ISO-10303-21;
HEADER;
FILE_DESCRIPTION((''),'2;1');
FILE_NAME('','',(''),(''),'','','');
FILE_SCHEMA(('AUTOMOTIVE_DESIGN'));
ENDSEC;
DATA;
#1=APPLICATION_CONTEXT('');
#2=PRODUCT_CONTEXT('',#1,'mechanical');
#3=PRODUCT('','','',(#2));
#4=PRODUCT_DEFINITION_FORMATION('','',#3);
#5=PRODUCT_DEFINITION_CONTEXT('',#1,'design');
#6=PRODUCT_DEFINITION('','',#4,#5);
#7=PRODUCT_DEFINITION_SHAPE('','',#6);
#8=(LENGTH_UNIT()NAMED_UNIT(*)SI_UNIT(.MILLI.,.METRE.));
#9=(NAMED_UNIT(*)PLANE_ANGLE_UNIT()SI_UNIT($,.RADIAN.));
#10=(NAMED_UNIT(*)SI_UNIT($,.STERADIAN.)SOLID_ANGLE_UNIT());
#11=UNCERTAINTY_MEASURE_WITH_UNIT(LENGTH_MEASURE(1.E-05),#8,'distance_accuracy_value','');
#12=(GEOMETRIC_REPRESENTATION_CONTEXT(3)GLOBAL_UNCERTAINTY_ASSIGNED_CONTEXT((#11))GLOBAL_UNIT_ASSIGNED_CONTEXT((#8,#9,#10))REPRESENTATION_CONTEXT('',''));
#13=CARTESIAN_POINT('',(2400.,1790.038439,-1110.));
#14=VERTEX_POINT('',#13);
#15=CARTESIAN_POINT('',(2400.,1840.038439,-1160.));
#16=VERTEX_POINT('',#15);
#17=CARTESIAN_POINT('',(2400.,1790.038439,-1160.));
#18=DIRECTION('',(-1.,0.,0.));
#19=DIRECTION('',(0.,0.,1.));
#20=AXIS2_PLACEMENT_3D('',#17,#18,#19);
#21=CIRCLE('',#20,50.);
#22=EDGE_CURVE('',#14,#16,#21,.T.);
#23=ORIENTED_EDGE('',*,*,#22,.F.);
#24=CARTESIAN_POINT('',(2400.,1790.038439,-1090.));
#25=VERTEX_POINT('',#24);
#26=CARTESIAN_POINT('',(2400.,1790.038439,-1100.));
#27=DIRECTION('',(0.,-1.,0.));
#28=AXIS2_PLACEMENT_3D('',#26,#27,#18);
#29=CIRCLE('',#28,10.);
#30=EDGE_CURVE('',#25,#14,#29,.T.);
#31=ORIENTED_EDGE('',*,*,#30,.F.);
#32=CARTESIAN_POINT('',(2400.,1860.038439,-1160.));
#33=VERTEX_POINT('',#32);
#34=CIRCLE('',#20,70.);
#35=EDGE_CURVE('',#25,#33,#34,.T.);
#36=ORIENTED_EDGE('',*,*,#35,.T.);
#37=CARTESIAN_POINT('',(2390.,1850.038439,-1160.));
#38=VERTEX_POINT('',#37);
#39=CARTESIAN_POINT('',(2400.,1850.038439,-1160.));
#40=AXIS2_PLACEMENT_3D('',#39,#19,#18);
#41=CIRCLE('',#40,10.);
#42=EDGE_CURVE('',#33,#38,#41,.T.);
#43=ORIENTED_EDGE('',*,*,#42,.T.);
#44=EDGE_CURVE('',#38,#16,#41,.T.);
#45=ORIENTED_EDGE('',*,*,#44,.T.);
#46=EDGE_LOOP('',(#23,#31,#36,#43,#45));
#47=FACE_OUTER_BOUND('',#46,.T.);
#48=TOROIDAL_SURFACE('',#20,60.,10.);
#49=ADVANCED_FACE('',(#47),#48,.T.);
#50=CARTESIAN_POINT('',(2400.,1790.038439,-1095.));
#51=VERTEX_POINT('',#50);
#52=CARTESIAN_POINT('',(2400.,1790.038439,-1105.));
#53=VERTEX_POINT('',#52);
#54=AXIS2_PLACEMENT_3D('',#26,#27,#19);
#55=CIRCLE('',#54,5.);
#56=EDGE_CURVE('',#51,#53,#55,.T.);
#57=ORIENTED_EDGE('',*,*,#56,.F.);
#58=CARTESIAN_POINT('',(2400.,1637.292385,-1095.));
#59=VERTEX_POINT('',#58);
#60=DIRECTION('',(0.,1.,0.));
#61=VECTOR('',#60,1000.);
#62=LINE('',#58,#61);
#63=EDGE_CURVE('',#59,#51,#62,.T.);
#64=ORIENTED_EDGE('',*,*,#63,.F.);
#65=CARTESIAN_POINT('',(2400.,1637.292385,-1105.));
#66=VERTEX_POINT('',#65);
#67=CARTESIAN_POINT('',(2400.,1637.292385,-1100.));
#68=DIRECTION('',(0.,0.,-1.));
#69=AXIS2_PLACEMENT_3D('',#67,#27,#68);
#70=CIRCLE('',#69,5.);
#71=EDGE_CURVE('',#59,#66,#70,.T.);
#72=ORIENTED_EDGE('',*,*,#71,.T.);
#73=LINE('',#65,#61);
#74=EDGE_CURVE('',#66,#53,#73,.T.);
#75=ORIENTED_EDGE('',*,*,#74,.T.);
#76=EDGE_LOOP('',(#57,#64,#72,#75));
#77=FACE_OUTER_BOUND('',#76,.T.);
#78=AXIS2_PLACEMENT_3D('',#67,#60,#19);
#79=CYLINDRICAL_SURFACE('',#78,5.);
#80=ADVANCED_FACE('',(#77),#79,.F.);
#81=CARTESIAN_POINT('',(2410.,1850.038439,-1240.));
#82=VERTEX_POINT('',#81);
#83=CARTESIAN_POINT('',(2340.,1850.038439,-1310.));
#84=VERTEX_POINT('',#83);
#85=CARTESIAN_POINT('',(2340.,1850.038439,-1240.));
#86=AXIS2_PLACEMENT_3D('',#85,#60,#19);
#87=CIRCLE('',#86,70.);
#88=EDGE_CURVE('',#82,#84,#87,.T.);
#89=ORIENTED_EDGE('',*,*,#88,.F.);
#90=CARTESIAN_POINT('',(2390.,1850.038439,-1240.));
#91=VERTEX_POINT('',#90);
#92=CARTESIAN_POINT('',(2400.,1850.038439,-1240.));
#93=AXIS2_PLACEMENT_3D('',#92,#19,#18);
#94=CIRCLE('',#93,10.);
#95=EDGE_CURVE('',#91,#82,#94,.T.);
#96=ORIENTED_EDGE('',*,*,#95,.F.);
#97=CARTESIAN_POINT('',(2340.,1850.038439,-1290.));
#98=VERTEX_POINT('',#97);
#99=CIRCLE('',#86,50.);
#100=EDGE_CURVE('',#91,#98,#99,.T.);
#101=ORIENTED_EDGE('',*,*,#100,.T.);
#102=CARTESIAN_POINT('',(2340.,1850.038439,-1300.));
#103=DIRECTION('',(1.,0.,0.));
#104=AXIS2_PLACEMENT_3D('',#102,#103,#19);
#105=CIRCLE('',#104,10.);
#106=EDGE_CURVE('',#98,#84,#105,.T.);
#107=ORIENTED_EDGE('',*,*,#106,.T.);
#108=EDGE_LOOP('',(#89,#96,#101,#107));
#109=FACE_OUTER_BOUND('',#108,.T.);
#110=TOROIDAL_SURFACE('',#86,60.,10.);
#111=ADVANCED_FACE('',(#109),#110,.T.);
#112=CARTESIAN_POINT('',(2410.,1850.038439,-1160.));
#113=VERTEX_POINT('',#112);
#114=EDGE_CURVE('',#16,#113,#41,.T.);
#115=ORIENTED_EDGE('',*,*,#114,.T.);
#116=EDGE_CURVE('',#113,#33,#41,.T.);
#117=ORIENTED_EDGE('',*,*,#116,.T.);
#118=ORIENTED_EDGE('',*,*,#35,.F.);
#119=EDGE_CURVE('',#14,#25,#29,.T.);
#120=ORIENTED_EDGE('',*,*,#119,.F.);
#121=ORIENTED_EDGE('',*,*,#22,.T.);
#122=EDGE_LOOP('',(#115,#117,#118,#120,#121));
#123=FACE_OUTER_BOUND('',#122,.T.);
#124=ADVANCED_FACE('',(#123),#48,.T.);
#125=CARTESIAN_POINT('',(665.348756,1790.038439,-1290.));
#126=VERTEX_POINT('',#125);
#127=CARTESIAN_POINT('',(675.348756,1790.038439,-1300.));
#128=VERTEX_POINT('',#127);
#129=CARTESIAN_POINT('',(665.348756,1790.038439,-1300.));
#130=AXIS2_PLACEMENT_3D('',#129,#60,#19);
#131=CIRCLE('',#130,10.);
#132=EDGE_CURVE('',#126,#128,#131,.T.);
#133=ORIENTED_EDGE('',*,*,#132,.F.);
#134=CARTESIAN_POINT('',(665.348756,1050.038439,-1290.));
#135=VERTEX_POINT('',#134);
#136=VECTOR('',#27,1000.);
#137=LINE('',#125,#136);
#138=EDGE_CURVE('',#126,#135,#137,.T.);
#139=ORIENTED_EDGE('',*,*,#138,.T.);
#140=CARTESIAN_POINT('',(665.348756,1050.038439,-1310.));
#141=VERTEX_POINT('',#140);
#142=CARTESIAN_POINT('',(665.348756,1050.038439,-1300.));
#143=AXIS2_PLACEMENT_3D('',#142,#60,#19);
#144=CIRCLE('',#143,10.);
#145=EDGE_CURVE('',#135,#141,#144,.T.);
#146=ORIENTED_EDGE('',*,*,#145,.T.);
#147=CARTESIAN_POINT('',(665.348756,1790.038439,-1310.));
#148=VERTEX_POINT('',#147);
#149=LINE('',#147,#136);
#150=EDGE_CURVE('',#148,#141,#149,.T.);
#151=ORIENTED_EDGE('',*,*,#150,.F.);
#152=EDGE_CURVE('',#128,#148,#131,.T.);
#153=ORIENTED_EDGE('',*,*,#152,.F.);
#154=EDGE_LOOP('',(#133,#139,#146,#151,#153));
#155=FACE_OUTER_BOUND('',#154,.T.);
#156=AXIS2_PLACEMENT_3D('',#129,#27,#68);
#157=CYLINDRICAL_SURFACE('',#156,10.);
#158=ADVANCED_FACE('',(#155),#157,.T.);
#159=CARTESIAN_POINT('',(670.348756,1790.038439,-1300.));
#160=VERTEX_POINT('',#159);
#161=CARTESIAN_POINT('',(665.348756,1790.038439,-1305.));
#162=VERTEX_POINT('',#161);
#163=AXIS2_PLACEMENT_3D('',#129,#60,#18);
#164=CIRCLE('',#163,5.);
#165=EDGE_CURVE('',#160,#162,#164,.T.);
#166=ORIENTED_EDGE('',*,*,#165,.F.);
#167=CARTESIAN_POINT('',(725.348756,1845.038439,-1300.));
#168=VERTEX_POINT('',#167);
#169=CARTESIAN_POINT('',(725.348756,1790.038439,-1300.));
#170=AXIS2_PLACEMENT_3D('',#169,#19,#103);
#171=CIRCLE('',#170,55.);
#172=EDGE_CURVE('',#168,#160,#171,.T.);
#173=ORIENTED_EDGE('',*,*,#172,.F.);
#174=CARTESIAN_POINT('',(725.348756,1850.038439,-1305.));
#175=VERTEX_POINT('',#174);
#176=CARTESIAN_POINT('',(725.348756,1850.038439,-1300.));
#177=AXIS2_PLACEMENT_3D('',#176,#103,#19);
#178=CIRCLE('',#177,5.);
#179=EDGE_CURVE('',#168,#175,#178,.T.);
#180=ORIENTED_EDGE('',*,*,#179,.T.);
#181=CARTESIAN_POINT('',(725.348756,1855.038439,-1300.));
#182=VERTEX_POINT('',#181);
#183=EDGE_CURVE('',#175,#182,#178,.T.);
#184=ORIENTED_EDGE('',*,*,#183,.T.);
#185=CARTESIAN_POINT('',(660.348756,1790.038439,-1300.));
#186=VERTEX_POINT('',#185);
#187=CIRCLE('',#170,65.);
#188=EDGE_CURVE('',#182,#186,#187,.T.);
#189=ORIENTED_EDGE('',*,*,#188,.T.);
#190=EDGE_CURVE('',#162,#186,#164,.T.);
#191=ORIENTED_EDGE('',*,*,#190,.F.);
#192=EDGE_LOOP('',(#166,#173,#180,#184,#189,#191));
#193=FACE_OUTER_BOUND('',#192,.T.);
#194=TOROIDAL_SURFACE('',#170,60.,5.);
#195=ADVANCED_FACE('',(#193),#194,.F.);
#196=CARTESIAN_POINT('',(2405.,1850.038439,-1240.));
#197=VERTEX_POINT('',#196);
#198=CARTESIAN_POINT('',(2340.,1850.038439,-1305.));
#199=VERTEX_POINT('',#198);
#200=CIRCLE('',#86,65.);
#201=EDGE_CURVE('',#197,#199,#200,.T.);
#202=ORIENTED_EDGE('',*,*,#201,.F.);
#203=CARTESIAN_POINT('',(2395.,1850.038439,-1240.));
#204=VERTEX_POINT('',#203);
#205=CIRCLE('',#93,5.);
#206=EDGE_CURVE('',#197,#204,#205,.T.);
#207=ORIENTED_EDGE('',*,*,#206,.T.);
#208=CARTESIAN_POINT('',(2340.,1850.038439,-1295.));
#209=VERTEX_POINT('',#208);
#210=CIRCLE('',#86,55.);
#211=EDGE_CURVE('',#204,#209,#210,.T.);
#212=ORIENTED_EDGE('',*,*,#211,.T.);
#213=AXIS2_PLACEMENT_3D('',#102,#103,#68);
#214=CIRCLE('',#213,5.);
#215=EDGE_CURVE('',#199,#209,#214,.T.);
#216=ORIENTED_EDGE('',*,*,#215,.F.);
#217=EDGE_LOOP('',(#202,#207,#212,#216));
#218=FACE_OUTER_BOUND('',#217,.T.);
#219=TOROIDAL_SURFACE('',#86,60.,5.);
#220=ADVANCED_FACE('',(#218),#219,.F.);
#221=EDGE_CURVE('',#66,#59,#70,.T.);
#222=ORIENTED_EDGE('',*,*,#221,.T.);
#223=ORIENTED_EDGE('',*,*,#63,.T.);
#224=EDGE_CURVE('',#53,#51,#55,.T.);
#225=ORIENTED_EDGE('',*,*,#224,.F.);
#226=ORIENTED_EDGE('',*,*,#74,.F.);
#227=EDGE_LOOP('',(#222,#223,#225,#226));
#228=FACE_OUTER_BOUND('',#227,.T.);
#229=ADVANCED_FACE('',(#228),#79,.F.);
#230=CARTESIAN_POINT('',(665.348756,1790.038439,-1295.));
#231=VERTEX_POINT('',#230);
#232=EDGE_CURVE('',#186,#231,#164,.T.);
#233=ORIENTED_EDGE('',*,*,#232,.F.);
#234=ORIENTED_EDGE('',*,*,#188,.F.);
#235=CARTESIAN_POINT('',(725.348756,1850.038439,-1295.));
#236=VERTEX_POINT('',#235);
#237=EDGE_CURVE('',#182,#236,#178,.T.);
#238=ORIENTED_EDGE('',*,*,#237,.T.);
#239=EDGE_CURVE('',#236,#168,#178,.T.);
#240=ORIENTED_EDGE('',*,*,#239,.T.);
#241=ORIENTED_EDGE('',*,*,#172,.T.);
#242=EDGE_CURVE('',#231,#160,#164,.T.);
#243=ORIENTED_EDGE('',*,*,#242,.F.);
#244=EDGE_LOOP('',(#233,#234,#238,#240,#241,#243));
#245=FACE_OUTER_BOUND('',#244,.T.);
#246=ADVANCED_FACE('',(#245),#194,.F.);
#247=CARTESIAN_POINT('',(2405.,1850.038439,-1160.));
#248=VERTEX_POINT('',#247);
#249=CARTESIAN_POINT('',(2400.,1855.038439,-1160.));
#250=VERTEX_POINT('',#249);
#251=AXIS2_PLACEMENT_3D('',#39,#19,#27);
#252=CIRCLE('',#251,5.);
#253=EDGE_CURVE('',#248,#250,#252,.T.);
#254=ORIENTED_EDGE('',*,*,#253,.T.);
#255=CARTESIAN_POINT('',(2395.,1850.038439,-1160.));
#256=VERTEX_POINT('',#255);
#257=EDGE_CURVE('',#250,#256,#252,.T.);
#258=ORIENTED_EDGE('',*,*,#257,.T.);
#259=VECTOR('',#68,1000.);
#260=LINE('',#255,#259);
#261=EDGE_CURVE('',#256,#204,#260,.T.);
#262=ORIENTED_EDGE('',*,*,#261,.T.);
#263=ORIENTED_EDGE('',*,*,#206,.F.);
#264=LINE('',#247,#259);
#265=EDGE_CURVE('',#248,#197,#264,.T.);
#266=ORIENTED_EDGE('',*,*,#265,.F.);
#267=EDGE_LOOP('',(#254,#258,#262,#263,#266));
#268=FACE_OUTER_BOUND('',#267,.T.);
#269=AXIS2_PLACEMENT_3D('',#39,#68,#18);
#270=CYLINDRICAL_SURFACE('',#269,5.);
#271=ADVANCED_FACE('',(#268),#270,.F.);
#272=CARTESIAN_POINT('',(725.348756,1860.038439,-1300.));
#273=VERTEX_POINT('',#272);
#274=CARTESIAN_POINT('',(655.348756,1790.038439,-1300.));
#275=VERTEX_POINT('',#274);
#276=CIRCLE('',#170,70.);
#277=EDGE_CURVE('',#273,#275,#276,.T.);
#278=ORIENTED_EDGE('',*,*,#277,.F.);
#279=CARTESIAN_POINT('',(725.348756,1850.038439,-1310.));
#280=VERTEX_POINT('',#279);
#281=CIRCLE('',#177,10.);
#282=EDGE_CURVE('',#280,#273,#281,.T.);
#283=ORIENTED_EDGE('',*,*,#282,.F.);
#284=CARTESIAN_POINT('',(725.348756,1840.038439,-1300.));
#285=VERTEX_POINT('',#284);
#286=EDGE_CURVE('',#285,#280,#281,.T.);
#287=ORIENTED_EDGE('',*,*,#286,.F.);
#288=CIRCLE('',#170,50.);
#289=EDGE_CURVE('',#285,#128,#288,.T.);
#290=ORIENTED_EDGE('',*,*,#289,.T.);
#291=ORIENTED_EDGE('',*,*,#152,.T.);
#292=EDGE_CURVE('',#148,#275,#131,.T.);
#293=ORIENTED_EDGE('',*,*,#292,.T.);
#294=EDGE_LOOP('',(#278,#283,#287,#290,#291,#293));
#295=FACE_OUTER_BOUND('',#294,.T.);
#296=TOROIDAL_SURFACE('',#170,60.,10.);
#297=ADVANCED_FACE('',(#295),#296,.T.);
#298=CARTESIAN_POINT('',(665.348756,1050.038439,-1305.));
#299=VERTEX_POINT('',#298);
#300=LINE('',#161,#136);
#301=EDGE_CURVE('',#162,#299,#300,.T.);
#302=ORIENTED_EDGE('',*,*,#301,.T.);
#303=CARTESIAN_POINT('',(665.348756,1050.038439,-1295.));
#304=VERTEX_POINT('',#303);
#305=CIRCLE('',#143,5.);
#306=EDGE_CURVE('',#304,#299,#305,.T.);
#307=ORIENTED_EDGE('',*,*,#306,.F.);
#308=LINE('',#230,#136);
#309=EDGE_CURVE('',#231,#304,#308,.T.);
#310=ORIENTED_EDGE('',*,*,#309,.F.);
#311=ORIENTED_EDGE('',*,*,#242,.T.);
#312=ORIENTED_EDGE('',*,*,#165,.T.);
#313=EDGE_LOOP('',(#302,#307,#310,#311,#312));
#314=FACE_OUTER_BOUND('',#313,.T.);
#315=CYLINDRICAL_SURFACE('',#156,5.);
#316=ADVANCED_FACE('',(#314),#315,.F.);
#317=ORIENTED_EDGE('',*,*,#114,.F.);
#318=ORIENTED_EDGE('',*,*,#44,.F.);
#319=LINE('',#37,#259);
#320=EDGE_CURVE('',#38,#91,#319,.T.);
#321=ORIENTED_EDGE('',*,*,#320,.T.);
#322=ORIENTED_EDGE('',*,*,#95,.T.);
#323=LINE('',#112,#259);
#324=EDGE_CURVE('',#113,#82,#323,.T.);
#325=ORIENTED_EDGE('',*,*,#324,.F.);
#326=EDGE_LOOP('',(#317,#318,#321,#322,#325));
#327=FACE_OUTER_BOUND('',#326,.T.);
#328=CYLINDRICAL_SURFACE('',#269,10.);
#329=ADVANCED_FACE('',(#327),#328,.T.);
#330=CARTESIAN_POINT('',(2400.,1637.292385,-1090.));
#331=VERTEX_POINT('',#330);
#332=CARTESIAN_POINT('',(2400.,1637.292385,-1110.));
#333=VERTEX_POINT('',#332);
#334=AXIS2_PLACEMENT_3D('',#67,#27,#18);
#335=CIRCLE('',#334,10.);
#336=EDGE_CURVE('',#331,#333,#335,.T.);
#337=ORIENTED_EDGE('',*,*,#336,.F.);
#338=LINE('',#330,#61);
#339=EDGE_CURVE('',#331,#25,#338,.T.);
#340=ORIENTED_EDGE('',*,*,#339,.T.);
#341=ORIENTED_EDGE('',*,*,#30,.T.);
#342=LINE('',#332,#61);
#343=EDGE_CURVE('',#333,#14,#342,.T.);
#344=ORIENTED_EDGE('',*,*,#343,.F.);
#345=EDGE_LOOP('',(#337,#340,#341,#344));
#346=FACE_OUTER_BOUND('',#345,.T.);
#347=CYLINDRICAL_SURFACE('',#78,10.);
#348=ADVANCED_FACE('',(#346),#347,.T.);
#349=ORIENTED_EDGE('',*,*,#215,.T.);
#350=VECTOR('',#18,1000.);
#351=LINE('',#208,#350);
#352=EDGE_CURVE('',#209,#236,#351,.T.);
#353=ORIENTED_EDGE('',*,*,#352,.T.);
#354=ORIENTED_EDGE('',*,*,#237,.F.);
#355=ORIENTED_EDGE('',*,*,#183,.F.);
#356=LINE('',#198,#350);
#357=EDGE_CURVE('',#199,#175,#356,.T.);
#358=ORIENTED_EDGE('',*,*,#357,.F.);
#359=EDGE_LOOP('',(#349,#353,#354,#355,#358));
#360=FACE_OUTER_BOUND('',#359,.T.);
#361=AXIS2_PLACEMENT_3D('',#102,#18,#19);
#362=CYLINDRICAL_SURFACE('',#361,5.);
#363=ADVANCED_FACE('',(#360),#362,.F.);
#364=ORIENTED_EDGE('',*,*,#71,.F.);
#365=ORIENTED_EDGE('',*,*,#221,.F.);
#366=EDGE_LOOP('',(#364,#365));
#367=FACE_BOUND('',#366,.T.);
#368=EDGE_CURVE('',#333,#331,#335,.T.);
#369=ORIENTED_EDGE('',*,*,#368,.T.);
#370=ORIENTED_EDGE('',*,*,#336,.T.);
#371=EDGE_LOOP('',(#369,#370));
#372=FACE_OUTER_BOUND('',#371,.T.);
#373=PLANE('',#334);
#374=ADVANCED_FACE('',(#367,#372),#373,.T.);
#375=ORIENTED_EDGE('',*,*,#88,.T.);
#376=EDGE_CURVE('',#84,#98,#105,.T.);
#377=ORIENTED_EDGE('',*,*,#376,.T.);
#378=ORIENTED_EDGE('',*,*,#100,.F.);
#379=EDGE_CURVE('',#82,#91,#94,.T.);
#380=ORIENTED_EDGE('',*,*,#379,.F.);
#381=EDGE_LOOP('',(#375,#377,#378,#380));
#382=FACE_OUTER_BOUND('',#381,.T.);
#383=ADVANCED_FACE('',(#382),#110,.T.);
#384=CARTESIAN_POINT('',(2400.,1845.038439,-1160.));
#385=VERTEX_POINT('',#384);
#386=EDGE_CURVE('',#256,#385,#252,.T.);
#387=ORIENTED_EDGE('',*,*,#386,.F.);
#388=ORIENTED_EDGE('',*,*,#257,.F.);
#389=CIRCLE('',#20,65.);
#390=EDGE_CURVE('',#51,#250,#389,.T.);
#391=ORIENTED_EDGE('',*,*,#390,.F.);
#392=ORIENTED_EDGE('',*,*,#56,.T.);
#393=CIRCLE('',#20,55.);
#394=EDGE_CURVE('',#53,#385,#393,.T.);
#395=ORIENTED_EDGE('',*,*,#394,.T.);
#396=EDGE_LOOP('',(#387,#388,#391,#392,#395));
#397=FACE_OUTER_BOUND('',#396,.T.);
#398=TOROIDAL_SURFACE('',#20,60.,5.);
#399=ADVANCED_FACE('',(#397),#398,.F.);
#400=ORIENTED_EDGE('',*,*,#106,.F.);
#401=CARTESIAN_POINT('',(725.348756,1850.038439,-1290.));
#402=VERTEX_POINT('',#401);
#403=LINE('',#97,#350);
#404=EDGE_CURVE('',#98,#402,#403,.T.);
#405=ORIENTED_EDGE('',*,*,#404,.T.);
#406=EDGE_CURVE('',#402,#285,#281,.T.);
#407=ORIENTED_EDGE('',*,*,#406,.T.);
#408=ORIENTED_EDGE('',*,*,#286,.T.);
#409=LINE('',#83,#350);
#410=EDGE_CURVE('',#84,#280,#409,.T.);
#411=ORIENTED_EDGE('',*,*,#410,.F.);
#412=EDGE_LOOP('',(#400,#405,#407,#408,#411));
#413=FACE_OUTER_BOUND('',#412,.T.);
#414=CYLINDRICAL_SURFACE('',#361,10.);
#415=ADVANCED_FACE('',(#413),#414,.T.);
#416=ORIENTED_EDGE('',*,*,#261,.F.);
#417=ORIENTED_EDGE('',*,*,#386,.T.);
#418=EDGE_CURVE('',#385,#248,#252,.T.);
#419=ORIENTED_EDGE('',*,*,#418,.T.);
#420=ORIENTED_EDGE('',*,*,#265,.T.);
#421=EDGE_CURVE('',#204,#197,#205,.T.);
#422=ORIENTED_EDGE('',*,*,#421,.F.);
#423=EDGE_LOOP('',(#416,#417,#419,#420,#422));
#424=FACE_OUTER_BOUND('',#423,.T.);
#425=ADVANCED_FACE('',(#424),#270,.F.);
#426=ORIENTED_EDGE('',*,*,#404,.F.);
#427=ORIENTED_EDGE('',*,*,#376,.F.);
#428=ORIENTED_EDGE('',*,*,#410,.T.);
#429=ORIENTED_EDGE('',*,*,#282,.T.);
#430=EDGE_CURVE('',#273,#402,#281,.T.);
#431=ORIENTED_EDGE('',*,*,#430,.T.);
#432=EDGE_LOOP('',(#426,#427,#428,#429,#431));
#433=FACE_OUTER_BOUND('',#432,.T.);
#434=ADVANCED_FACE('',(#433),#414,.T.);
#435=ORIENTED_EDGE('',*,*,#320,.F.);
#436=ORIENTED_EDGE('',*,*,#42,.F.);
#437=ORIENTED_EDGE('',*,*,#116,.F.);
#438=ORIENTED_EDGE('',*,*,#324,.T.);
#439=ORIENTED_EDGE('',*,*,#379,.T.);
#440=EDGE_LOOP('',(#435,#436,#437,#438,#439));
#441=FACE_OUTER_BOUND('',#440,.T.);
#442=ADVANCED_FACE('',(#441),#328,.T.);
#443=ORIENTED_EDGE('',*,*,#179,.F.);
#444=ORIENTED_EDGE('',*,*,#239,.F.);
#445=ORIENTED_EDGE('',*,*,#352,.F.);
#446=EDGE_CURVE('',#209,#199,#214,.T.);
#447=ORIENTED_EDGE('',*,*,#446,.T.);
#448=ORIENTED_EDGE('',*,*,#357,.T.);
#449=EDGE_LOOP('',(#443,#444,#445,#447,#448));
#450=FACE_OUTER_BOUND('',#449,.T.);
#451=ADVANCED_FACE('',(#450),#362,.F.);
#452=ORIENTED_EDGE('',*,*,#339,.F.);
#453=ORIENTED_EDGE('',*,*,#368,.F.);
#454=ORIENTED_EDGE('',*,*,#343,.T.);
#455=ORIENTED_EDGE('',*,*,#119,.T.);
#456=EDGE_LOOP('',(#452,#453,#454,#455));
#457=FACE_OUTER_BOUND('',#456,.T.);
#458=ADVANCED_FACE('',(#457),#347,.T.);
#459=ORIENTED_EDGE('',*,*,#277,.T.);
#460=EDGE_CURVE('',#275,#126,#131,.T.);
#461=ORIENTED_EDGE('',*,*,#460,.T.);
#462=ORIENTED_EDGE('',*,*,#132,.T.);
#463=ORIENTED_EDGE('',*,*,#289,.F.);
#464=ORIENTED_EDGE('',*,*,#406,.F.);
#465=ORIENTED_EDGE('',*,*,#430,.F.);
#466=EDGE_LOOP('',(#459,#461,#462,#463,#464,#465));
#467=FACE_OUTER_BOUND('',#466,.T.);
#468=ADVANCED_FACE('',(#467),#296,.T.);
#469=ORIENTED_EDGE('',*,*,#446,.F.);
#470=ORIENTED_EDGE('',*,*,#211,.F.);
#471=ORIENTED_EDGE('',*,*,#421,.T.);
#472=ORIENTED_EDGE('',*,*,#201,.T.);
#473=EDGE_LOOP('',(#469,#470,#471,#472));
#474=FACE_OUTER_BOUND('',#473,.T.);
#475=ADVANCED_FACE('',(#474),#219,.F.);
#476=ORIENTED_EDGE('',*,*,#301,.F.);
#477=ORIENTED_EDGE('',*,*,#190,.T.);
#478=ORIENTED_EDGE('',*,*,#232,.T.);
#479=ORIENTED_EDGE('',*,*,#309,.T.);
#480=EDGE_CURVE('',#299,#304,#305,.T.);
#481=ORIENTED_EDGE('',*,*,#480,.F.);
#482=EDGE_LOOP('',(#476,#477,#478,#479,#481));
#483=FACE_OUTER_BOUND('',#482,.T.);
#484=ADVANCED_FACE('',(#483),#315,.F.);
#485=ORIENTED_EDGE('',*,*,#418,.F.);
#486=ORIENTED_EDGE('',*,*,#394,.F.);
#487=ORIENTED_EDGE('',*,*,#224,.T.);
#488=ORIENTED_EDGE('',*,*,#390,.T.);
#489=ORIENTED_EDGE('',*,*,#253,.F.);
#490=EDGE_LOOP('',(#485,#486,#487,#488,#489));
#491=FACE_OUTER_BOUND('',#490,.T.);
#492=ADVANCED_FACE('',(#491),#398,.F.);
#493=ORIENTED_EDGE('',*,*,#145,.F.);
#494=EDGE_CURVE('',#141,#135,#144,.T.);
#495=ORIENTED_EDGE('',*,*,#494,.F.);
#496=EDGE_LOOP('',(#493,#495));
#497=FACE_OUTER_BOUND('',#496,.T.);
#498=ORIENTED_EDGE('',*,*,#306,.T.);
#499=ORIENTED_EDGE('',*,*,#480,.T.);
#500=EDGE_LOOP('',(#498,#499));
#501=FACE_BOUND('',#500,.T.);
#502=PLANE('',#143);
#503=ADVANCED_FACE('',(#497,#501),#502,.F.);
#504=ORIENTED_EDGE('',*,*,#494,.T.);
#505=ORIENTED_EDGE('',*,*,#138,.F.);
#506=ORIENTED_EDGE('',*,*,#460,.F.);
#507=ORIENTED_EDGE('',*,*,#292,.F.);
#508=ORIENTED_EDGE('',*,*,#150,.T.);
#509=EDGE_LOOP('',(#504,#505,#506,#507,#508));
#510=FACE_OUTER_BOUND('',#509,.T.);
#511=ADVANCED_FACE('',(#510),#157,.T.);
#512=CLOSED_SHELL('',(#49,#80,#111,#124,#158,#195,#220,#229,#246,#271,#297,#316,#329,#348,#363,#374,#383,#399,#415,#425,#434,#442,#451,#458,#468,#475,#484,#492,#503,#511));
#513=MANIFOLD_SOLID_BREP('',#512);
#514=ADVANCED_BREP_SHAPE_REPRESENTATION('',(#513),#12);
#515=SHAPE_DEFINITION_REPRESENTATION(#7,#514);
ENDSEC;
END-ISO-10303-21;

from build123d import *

# Parameters (mm, degrees)
SWEEP_THIN1_PROFILE_R   = 10
SWEEP_THIN1_PROFILE_R_2 = 5


with BuildPart() as part:
    # Sweep-Thin1: sweep along a curve in space
    with BuildLine() as sweep_thin1_path:
        Line((2400, 1637.292385154, -1100), (2400, 1790.038439201, -1100))
        ThreePointArc((2400, 1790.038439201, -1100), (2400, 1832.464846073, -1117.573593129), (2400, 1850.038439201, -1160))
        Line((2400, 1850.038439201, -1160), (2400, 1850.038439201, -1240))
        ThreePointArc((2400, 1850.038439201, -1240), (2382.426406871, 1850.038439201, -1282.426406871), (2340, 1850.038439201, -1300))
        Line((2340, 1850.038439201, -1300), (725.34875551, 1850.038439201, -1300))
        ThreePointArc((725.34875551, 1850.038439201, -1300), (682.922348639, 1832.464846073, -1300), (665.34875551, 1790.038439201, -1300))
        Line((665.34875551, 1790.038439201, -1300), (665.34875551, 1050.038439201, -1300))
    # Sweep-Thin1 profile (on start of the path) → Sweep-Thin1 (sweep)
    with BuildSketch(Plane(origin=(2400, 1637.292385154, -1100), x_dir=(0, 0, 1), z_dir=(0, 1, 0))):
        Circle(SWEEP_THIN1_PROFILE_R)
        Circle(SWEEP_THIN1_PROFILE_R_2, mode=Mode.SUBTRACT)
    sweep(path=sweep_thin1_path.line)


solid = part.part
